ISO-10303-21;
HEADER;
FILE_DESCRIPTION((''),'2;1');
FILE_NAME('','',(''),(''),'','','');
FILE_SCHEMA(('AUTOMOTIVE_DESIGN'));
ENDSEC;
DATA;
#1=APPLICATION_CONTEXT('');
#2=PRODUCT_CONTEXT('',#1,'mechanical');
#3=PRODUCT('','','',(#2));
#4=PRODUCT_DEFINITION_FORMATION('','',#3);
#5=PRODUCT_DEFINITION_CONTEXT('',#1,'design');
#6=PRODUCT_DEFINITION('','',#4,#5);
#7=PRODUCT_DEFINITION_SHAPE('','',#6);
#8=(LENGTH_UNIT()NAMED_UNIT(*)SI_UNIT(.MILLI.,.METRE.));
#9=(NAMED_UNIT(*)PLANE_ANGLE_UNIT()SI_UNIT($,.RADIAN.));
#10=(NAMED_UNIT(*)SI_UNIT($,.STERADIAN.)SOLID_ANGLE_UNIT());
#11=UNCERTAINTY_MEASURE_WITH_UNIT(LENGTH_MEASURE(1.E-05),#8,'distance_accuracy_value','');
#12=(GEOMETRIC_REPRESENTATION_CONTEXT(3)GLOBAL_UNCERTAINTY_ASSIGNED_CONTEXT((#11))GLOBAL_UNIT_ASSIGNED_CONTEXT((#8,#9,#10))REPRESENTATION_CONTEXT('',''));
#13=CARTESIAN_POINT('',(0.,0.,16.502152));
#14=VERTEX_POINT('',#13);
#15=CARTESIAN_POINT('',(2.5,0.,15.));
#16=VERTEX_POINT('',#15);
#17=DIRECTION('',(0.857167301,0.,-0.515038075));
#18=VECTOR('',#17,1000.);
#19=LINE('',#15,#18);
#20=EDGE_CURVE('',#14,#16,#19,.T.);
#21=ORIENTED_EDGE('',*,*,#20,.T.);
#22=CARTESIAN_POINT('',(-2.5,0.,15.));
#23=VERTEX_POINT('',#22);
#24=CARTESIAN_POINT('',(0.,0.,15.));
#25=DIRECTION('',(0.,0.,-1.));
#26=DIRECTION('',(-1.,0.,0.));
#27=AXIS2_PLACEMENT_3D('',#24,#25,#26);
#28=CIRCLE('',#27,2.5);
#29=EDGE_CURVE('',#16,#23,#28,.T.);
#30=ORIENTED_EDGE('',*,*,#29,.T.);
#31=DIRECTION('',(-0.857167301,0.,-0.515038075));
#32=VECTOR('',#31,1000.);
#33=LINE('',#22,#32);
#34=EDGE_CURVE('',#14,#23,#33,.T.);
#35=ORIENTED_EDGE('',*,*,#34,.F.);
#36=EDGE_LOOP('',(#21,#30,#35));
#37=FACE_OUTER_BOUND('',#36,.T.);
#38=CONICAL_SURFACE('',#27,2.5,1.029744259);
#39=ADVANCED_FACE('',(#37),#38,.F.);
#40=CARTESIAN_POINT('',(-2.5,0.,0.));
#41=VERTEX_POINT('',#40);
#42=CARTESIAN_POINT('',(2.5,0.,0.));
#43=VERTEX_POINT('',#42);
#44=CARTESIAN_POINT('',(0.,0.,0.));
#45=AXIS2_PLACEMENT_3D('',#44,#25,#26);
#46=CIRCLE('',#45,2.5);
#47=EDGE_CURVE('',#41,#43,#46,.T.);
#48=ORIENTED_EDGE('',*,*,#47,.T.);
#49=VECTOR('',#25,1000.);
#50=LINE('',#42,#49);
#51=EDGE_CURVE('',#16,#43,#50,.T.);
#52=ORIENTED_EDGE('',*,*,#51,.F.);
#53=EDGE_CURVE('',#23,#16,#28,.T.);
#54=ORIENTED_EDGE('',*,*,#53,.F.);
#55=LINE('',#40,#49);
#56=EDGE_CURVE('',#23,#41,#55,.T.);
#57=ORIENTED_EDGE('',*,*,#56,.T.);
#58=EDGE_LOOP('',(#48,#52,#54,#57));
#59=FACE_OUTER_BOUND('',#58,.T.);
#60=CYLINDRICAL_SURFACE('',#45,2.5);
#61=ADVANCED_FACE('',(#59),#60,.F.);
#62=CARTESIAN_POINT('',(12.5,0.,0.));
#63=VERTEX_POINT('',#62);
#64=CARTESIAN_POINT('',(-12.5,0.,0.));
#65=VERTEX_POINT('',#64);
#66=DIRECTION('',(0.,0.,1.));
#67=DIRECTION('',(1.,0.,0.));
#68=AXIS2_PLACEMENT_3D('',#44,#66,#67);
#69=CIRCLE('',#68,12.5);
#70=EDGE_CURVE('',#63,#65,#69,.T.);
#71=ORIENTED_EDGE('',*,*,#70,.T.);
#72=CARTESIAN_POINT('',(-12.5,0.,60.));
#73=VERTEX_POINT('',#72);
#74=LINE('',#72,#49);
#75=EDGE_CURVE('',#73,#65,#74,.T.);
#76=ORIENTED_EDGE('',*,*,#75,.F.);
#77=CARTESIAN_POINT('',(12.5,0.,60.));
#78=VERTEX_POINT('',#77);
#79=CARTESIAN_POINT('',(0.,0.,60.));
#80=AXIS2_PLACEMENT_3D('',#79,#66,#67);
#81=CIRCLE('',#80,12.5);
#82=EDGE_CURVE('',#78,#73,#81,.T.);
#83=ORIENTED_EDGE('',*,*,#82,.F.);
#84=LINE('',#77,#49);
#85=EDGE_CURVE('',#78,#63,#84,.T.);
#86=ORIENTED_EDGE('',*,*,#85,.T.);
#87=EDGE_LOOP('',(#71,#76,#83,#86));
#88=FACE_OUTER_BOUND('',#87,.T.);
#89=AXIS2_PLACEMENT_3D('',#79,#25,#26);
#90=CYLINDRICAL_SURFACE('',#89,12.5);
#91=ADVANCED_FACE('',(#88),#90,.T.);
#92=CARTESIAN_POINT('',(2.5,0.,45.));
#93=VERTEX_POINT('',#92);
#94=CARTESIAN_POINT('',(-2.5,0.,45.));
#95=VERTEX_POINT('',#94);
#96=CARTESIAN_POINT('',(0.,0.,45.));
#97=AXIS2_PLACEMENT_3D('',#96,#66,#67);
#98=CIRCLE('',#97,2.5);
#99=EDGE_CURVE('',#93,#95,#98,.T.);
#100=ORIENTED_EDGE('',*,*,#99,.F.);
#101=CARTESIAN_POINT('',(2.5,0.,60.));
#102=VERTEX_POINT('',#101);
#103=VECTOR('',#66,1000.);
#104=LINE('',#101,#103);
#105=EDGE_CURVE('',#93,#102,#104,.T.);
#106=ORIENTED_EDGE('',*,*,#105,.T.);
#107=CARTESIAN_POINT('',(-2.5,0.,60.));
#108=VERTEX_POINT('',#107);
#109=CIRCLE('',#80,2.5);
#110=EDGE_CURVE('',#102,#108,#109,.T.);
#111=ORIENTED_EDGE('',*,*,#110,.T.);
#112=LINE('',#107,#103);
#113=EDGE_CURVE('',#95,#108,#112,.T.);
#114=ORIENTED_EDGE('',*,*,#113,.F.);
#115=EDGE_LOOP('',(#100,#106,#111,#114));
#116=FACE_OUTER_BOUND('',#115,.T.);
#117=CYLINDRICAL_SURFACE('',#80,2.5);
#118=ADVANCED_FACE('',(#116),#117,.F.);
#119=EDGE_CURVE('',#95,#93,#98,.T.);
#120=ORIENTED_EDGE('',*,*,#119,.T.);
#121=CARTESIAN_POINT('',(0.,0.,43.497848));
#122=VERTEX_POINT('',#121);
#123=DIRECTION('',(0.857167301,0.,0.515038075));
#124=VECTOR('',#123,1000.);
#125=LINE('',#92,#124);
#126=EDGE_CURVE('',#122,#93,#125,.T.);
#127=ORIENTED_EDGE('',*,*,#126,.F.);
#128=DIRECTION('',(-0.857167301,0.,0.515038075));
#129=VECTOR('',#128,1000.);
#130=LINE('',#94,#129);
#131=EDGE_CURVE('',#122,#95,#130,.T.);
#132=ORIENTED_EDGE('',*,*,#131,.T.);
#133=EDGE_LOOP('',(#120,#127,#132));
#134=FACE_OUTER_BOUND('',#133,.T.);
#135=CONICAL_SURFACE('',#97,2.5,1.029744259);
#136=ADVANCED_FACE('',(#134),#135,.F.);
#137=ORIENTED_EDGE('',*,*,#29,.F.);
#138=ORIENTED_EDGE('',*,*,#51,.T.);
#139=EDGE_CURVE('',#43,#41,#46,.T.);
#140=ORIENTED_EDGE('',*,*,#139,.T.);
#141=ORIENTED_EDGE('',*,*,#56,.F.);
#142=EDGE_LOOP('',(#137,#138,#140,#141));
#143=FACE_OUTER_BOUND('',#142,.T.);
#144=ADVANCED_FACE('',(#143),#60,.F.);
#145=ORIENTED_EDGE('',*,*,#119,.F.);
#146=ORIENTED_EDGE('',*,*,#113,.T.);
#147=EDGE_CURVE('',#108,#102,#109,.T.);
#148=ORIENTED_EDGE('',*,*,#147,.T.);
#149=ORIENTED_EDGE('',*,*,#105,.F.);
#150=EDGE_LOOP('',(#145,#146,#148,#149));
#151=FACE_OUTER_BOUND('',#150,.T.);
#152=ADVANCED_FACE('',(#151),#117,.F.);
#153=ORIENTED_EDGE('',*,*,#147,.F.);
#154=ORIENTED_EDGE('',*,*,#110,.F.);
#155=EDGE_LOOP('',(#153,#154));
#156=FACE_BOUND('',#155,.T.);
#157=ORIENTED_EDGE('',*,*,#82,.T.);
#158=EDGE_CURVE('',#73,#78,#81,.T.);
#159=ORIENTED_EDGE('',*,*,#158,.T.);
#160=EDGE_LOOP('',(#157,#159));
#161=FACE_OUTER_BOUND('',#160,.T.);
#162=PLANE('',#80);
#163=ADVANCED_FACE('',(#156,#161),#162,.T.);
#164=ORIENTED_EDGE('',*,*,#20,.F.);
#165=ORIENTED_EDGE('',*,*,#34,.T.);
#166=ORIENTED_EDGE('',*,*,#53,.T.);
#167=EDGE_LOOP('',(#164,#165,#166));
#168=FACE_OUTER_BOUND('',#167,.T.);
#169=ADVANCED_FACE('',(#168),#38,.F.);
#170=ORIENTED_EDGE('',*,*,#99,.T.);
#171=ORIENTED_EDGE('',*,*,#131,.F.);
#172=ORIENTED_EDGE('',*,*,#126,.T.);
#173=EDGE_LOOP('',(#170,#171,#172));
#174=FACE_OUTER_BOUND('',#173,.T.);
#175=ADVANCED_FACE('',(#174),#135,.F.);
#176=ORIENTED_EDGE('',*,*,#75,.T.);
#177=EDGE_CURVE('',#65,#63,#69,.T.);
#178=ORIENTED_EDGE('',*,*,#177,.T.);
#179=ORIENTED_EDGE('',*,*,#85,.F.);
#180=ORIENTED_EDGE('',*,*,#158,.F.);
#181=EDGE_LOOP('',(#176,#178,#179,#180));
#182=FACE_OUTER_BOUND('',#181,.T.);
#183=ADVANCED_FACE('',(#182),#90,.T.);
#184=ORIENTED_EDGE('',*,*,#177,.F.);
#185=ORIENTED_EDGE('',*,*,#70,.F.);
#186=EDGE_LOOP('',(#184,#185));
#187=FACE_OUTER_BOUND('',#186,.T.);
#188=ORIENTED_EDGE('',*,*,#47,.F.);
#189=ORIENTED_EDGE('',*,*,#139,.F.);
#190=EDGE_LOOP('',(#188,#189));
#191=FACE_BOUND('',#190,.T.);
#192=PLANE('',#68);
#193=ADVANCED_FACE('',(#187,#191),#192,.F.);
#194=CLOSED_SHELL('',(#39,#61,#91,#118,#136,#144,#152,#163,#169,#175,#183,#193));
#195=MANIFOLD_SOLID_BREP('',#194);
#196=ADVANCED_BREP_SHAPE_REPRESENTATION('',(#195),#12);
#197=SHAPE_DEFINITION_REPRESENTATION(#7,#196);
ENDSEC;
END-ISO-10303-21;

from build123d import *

# Parameters (mm, degrees)
SKETCH_1_R             = 12.5
BOSS_EXTRUDE_1_DEPTH   = 60
M6_TAPPED_HOLE_1_D     = 5
M6_TAPPED_HOLE_1_DEPTH = 15
M6_TAPPED_HOLE_1_TIP   = 1.502151548
M6_TAPPED_HOLE_2_D     = 5
M6_TAPPED_HOLE_2_DEPTH = 15
M6_TAPPED_HOLE_2_TIP   = 1.502151548


with BuildPart() as part:
    # Sketch 1 → Boss-Extrude 1 (new body)
    with BuildSketch(Plane.XY):
        Circle(SKETCH_1_R)
    extrude(amount=BOSS_EXTRUDE_1_DEPTH)

    # M6 Tapped Hole 1
    with Locations(Plane.XY.offset(60)):
        with Locations((0, 0)):
            Hole(M6_TAPPED_HOLE_1_D / 2, depth=M6_TAPPED_HOLE_1_DEPTH)
            with Locations((0, 0, -(M6_TAPPED_HOLE_1_DEPTH + M6_TAPPED_HOLE_1_TIP / 2))):  # 118° drill point
                Cone(0, M6_TAPPED_HOLE_1_D / 2, M6_TAPPED_HOLE_1_TIP, mode=Mode.SUBTRACT)

    # M6 Tapped Hole 2
    with Locations(Plane(origin=(0, 0, 0), x_dir=(-1, 0, 0), z_dir=(0, 0, -1))):
        with Locations((0, 0)):
            Hole(M6_TAPPED_HOLE_2_D / 2, depth=M6_TAPPED_HOLE_2_DEPTH)
            with Locations((0, 0, -(M6_TAPPED_HOLE_2_DEPTH + M6_TAPPED_HOLE_2_TIP / 2))):  # 118° drill point
                Cone(0, M6_TAPPED_HOLE_2_D / 2, M6_TAPPED_HOLE_2_TIP, mode=Mode.SUBTRACT)


solid = part.part
